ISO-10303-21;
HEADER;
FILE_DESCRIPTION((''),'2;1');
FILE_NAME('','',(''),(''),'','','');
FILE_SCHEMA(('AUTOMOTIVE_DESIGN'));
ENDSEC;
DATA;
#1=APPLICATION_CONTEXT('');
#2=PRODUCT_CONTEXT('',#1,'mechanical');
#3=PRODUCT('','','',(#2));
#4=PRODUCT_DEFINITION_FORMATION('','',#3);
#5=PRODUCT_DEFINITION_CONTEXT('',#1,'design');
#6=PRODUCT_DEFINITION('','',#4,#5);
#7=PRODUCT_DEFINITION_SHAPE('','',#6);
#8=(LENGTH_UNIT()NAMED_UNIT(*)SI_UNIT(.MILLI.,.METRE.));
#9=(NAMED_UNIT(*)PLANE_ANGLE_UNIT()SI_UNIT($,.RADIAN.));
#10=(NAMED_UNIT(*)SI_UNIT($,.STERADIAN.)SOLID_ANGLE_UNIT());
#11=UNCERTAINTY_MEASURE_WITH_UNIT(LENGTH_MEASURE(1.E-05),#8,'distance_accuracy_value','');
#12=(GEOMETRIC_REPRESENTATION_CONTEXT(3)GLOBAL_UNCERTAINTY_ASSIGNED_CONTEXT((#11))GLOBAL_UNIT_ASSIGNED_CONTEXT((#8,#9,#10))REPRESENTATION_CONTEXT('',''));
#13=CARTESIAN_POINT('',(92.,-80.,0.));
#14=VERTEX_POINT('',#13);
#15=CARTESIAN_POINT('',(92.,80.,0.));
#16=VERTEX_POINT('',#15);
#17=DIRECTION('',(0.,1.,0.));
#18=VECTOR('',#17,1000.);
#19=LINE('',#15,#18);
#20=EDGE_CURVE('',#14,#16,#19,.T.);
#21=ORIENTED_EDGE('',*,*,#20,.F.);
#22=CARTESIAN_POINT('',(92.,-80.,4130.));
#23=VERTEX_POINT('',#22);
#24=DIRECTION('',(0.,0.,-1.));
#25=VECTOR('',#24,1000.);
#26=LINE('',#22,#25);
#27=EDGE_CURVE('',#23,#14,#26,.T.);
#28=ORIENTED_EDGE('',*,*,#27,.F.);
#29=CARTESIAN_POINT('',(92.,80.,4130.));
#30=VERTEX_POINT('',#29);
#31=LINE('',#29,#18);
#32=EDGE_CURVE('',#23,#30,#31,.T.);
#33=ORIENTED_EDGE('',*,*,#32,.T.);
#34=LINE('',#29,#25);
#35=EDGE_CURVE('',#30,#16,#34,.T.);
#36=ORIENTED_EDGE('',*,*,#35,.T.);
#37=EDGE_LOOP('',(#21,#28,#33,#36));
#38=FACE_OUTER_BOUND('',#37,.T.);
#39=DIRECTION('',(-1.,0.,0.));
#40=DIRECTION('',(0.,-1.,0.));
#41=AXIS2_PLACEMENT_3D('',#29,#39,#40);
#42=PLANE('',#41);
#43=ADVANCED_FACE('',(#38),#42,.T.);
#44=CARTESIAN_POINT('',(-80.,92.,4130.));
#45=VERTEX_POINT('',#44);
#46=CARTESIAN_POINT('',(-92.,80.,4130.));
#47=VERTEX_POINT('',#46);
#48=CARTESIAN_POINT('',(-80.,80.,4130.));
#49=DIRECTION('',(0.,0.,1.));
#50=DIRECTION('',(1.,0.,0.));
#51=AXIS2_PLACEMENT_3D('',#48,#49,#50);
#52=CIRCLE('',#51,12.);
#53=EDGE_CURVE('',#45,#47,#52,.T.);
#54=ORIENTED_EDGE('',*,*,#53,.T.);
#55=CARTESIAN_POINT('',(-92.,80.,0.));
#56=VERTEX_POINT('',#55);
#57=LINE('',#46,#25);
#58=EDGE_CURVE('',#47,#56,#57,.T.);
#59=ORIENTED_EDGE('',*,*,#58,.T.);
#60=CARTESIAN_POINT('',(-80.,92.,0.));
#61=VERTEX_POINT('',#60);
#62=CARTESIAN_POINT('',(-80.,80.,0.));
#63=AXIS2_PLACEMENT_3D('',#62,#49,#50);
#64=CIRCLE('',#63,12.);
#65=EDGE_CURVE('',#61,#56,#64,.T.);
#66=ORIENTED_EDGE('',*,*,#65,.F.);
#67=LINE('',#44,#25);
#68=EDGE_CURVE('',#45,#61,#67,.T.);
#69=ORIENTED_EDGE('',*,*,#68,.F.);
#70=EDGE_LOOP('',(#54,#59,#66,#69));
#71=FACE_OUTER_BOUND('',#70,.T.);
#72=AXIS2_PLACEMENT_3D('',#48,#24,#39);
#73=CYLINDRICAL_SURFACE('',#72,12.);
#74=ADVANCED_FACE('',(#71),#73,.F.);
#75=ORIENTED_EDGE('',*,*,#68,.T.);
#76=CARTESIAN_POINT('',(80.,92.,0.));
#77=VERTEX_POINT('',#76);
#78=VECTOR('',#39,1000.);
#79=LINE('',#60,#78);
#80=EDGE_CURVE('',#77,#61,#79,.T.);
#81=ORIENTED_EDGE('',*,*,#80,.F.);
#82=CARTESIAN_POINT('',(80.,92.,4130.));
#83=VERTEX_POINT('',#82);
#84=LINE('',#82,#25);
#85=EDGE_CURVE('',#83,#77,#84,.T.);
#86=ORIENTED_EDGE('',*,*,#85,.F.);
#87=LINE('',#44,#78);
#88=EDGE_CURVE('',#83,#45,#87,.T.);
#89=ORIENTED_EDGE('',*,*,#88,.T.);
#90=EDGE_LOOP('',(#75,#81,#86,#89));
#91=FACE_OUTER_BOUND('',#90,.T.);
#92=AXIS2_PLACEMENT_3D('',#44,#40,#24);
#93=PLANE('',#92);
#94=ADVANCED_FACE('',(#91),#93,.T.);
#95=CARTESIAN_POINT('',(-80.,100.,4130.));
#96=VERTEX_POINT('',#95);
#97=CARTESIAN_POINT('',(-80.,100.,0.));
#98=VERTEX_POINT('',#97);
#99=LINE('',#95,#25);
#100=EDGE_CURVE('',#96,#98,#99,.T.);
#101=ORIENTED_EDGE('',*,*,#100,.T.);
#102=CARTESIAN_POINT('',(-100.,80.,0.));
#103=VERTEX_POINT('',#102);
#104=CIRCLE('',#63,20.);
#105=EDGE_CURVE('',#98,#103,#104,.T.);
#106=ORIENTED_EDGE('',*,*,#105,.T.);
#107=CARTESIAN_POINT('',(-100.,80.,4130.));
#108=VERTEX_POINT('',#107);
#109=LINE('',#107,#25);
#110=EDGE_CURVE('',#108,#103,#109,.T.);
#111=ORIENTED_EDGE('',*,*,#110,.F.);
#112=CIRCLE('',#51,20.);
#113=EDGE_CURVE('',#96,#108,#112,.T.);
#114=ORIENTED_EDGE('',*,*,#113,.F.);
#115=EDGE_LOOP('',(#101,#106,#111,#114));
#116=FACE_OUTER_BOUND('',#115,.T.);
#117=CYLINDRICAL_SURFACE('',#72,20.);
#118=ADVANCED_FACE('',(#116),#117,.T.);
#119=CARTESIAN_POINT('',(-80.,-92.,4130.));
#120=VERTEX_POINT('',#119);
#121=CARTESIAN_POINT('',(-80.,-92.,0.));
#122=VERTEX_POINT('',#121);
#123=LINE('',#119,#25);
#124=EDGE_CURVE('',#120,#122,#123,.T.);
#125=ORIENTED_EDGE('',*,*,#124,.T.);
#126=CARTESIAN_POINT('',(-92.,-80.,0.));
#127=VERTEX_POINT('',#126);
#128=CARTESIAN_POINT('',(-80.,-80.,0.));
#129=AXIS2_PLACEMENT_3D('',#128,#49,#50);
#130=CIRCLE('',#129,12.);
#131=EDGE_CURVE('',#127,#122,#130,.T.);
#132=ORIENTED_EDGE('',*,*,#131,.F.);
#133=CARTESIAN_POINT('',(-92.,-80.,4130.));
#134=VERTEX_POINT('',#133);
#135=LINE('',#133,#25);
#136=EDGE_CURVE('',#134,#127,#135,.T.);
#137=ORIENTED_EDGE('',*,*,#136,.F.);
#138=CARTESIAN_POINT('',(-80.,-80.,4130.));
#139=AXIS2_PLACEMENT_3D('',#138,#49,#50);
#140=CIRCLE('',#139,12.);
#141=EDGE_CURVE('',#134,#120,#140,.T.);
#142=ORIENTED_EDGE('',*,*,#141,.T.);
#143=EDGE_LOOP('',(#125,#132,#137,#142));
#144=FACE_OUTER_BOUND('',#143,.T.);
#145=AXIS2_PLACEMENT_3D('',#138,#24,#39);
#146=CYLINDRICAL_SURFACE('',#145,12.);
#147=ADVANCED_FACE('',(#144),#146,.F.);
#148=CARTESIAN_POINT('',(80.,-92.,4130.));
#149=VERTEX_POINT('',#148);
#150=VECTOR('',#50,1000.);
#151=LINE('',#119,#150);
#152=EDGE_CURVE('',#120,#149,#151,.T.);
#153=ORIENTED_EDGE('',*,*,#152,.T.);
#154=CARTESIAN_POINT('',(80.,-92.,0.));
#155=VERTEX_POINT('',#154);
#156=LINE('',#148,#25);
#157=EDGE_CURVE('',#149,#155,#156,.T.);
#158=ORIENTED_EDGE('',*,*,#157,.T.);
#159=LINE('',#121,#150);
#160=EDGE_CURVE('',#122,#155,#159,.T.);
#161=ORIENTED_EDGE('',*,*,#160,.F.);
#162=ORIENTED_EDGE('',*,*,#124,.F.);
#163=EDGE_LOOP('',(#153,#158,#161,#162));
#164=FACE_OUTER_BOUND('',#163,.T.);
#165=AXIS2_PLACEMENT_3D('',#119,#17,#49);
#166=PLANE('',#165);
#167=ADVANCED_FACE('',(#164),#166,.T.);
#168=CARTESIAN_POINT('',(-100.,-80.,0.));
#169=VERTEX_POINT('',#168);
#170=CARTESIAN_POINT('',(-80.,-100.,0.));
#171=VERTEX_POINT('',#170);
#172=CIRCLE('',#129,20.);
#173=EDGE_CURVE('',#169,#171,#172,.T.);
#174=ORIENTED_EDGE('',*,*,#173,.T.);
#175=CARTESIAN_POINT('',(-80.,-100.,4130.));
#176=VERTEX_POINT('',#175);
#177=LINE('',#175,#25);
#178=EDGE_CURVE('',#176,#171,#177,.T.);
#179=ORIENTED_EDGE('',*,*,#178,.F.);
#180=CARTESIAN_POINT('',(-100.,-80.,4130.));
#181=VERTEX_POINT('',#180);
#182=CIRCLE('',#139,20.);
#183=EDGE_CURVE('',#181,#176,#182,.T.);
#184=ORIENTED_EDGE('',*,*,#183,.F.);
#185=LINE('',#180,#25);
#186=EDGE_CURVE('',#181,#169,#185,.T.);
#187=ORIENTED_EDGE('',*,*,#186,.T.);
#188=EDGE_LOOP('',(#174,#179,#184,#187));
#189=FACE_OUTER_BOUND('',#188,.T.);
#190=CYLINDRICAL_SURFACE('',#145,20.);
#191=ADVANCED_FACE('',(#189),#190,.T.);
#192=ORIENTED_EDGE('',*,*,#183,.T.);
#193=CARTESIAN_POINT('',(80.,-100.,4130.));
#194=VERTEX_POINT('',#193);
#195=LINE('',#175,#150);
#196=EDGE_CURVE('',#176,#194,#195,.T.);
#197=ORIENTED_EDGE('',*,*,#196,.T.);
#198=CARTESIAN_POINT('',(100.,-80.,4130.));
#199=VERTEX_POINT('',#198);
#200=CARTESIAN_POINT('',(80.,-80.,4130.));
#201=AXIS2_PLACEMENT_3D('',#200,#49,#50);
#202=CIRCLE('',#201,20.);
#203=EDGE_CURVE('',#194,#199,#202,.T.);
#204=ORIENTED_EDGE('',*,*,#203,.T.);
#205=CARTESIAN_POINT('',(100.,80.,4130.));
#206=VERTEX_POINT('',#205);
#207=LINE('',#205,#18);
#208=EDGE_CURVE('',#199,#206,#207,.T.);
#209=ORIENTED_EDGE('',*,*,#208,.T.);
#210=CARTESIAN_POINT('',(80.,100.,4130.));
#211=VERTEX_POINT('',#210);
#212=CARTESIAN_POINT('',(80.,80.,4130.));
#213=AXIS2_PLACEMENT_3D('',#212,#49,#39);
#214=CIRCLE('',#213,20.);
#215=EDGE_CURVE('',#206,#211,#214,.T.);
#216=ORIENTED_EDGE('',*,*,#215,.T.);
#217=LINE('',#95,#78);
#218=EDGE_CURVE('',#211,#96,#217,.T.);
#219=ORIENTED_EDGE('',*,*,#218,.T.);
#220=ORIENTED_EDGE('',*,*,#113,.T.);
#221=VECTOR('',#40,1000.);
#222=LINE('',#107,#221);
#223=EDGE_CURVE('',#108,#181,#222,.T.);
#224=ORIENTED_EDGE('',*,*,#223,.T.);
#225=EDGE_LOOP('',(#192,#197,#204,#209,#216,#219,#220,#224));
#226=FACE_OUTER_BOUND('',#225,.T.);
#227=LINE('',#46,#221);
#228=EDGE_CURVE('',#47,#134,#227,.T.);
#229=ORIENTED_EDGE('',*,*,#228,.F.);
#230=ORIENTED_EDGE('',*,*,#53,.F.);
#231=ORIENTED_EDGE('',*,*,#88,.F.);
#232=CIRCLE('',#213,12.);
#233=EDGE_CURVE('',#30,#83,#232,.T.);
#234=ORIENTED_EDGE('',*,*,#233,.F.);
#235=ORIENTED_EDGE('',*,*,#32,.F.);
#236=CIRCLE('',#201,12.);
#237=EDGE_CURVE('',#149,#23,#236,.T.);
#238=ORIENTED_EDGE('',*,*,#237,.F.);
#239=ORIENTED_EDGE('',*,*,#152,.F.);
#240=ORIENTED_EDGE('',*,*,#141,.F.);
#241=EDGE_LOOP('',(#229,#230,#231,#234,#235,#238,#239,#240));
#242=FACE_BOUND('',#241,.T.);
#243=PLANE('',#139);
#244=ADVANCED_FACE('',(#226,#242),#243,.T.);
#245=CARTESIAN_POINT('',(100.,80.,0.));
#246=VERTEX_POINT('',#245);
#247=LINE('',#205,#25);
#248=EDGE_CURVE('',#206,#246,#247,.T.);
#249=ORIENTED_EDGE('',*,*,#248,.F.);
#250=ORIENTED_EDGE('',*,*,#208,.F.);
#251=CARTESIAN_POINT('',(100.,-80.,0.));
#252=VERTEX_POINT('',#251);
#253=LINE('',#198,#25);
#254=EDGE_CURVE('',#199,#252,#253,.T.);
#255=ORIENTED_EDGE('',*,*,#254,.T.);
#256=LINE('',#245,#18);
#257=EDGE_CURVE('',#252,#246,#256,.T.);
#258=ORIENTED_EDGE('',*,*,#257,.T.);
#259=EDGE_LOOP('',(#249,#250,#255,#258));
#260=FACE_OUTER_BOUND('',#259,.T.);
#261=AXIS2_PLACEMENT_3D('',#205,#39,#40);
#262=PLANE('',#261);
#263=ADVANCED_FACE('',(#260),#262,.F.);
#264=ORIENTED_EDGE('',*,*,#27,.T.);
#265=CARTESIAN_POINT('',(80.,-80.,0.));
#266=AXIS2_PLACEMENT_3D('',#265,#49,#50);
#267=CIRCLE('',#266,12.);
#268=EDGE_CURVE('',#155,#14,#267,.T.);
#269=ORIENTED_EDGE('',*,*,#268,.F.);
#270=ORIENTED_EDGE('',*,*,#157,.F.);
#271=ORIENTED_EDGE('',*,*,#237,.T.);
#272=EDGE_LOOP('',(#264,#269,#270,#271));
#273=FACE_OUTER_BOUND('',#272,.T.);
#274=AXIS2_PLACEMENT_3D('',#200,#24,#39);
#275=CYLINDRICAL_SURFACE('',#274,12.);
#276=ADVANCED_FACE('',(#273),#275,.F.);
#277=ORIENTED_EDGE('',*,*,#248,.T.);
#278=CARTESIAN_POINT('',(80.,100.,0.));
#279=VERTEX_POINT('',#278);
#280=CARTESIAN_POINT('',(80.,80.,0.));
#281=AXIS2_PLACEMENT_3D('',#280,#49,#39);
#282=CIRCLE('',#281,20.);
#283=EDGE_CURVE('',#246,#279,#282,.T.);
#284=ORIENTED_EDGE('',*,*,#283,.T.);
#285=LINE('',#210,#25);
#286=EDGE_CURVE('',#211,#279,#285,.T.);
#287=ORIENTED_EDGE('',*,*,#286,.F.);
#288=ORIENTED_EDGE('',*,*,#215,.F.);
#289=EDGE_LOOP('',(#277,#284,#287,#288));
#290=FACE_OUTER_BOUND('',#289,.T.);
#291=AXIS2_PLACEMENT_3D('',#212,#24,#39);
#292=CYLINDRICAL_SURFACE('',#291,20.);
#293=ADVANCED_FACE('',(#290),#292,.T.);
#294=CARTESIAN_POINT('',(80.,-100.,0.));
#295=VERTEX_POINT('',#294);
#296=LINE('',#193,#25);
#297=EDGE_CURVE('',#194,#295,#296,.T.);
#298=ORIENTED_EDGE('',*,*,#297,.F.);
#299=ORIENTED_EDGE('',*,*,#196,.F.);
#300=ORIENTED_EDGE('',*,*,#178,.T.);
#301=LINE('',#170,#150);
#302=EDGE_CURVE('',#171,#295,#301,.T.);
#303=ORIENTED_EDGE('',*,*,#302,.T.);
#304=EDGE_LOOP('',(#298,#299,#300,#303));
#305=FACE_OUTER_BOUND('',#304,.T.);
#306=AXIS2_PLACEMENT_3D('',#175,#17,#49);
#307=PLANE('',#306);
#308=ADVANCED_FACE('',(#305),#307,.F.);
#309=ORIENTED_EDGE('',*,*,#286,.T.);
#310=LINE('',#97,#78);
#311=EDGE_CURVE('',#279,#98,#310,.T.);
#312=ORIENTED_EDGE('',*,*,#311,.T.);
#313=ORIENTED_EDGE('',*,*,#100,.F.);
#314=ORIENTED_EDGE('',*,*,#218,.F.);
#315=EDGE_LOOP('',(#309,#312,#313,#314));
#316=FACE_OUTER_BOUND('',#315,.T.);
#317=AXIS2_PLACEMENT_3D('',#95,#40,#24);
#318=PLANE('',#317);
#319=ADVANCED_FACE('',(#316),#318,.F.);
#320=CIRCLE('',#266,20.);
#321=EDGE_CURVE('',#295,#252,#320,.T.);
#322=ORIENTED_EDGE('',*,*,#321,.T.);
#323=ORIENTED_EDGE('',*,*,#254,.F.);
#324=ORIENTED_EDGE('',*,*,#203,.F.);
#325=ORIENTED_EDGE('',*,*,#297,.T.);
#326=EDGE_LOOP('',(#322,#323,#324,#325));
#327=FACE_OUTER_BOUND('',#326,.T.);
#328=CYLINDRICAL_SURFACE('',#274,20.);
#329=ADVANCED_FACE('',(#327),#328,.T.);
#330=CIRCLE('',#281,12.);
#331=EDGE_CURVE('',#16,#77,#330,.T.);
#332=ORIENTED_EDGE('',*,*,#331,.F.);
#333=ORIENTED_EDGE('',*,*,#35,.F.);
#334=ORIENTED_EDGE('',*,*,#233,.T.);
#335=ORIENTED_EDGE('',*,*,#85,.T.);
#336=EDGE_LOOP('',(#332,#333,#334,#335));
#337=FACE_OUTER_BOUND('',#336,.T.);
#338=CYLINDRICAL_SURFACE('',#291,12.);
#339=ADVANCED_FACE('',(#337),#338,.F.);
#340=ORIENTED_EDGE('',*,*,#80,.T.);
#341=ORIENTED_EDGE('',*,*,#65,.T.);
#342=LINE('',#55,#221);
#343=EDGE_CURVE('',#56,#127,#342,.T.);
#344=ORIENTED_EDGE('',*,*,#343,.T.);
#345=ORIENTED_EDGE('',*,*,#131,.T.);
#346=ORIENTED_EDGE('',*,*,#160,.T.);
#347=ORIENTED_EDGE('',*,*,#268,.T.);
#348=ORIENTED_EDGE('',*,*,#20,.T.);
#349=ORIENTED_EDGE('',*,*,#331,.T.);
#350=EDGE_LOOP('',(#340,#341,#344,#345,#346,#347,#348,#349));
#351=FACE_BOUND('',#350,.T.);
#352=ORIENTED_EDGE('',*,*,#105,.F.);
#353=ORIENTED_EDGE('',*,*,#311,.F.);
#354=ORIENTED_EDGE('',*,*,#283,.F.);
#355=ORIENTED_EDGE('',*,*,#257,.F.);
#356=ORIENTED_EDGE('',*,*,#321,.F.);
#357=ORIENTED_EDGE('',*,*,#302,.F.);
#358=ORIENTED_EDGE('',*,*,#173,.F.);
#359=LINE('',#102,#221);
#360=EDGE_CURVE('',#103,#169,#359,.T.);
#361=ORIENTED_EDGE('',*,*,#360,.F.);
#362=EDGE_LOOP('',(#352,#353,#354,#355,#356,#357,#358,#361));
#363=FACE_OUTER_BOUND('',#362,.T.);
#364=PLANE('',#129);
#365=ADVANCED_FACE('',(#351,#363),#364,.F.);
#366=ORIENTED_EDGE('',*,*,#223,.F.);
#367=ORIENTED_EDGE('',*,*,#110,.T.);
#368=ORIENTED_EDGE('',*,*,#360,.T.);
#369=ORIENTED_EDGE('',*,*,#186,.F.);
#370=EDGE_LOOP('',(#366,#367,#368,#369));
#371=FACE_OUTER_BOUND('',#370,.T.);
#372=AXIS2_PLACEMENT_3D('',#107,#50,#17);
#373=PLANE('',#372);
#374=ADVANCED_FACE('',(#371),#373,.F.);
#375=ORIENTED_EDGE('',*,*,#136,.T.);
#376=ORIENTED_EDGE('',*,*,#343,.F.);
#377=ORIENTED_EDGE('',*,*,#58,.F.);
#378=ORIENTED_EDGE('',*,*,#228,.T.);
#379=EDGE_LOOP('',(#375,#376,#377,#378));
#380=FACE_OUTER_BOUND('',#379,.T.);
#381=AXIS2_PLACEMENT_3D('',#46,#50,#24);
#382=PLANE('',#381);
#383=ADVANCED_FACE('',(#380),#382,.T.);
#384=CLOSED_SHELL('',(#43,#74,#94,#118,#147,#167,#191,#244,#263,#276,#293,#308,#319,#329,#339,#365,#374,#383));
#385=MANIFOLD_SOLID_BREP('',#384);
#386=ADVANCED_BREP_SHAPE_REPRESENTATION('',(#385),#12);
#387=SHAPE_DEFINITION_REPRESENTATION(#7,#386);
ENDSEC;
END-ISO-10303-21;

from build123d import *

# Parameters (mm, degrees)
BOSS_EXTRUDE1_DEPTH = 4130


with BuildPart() as part:
    # Sketch1 → Boss-Extrude1 (new body)
    with BuildSketch(Plane.XY):
        with BuildLine():
            Line((-80, 100), (80, 100))
            ThreePointArc((80, 100), (94.142135624, 94.142135624), (100, 80))
            Line((100, 80), (100, -80))
            ThreePointArc((100, -80), (94.142135624, -94.142135624), (80, -100))
            Line((80, -100), (-80, -100))
            ThreePointArc((-80, -100), (-94.142135624, -94.142135624), (-100, -80))
            Line((-100, -80), (-100, 80))
            ThreePointArc((-100, 80), (-94.142135624, 94.142135624), (-80, 100))
        make_face()
        with BuildLine():
            Line((-92, 80), (-92, -80))
            ThreePointArc((-92, -80), (-88.485281374, -88.485281374), (-80, -92))
            Line((-80, -92), (80, -92))
            ThreePointArc((80, -92), (88.485281374, -88.485281374), (92, -80))
            Line((92, -80), (92, 80))
            ThreePointArc((92, 80), (88.485281374, 88.485281374), (80, 92))
            Line((80, 92), (-80, 92))
            ThreePointArc((-80, 92), (-88.485281374, 88.485281374), (-92, 80))
        make_face(mode=Mode.SUBTRACT)
    extrude(amount=BOSS_EXTRUDE1_DEPTH)


solid = part.part
